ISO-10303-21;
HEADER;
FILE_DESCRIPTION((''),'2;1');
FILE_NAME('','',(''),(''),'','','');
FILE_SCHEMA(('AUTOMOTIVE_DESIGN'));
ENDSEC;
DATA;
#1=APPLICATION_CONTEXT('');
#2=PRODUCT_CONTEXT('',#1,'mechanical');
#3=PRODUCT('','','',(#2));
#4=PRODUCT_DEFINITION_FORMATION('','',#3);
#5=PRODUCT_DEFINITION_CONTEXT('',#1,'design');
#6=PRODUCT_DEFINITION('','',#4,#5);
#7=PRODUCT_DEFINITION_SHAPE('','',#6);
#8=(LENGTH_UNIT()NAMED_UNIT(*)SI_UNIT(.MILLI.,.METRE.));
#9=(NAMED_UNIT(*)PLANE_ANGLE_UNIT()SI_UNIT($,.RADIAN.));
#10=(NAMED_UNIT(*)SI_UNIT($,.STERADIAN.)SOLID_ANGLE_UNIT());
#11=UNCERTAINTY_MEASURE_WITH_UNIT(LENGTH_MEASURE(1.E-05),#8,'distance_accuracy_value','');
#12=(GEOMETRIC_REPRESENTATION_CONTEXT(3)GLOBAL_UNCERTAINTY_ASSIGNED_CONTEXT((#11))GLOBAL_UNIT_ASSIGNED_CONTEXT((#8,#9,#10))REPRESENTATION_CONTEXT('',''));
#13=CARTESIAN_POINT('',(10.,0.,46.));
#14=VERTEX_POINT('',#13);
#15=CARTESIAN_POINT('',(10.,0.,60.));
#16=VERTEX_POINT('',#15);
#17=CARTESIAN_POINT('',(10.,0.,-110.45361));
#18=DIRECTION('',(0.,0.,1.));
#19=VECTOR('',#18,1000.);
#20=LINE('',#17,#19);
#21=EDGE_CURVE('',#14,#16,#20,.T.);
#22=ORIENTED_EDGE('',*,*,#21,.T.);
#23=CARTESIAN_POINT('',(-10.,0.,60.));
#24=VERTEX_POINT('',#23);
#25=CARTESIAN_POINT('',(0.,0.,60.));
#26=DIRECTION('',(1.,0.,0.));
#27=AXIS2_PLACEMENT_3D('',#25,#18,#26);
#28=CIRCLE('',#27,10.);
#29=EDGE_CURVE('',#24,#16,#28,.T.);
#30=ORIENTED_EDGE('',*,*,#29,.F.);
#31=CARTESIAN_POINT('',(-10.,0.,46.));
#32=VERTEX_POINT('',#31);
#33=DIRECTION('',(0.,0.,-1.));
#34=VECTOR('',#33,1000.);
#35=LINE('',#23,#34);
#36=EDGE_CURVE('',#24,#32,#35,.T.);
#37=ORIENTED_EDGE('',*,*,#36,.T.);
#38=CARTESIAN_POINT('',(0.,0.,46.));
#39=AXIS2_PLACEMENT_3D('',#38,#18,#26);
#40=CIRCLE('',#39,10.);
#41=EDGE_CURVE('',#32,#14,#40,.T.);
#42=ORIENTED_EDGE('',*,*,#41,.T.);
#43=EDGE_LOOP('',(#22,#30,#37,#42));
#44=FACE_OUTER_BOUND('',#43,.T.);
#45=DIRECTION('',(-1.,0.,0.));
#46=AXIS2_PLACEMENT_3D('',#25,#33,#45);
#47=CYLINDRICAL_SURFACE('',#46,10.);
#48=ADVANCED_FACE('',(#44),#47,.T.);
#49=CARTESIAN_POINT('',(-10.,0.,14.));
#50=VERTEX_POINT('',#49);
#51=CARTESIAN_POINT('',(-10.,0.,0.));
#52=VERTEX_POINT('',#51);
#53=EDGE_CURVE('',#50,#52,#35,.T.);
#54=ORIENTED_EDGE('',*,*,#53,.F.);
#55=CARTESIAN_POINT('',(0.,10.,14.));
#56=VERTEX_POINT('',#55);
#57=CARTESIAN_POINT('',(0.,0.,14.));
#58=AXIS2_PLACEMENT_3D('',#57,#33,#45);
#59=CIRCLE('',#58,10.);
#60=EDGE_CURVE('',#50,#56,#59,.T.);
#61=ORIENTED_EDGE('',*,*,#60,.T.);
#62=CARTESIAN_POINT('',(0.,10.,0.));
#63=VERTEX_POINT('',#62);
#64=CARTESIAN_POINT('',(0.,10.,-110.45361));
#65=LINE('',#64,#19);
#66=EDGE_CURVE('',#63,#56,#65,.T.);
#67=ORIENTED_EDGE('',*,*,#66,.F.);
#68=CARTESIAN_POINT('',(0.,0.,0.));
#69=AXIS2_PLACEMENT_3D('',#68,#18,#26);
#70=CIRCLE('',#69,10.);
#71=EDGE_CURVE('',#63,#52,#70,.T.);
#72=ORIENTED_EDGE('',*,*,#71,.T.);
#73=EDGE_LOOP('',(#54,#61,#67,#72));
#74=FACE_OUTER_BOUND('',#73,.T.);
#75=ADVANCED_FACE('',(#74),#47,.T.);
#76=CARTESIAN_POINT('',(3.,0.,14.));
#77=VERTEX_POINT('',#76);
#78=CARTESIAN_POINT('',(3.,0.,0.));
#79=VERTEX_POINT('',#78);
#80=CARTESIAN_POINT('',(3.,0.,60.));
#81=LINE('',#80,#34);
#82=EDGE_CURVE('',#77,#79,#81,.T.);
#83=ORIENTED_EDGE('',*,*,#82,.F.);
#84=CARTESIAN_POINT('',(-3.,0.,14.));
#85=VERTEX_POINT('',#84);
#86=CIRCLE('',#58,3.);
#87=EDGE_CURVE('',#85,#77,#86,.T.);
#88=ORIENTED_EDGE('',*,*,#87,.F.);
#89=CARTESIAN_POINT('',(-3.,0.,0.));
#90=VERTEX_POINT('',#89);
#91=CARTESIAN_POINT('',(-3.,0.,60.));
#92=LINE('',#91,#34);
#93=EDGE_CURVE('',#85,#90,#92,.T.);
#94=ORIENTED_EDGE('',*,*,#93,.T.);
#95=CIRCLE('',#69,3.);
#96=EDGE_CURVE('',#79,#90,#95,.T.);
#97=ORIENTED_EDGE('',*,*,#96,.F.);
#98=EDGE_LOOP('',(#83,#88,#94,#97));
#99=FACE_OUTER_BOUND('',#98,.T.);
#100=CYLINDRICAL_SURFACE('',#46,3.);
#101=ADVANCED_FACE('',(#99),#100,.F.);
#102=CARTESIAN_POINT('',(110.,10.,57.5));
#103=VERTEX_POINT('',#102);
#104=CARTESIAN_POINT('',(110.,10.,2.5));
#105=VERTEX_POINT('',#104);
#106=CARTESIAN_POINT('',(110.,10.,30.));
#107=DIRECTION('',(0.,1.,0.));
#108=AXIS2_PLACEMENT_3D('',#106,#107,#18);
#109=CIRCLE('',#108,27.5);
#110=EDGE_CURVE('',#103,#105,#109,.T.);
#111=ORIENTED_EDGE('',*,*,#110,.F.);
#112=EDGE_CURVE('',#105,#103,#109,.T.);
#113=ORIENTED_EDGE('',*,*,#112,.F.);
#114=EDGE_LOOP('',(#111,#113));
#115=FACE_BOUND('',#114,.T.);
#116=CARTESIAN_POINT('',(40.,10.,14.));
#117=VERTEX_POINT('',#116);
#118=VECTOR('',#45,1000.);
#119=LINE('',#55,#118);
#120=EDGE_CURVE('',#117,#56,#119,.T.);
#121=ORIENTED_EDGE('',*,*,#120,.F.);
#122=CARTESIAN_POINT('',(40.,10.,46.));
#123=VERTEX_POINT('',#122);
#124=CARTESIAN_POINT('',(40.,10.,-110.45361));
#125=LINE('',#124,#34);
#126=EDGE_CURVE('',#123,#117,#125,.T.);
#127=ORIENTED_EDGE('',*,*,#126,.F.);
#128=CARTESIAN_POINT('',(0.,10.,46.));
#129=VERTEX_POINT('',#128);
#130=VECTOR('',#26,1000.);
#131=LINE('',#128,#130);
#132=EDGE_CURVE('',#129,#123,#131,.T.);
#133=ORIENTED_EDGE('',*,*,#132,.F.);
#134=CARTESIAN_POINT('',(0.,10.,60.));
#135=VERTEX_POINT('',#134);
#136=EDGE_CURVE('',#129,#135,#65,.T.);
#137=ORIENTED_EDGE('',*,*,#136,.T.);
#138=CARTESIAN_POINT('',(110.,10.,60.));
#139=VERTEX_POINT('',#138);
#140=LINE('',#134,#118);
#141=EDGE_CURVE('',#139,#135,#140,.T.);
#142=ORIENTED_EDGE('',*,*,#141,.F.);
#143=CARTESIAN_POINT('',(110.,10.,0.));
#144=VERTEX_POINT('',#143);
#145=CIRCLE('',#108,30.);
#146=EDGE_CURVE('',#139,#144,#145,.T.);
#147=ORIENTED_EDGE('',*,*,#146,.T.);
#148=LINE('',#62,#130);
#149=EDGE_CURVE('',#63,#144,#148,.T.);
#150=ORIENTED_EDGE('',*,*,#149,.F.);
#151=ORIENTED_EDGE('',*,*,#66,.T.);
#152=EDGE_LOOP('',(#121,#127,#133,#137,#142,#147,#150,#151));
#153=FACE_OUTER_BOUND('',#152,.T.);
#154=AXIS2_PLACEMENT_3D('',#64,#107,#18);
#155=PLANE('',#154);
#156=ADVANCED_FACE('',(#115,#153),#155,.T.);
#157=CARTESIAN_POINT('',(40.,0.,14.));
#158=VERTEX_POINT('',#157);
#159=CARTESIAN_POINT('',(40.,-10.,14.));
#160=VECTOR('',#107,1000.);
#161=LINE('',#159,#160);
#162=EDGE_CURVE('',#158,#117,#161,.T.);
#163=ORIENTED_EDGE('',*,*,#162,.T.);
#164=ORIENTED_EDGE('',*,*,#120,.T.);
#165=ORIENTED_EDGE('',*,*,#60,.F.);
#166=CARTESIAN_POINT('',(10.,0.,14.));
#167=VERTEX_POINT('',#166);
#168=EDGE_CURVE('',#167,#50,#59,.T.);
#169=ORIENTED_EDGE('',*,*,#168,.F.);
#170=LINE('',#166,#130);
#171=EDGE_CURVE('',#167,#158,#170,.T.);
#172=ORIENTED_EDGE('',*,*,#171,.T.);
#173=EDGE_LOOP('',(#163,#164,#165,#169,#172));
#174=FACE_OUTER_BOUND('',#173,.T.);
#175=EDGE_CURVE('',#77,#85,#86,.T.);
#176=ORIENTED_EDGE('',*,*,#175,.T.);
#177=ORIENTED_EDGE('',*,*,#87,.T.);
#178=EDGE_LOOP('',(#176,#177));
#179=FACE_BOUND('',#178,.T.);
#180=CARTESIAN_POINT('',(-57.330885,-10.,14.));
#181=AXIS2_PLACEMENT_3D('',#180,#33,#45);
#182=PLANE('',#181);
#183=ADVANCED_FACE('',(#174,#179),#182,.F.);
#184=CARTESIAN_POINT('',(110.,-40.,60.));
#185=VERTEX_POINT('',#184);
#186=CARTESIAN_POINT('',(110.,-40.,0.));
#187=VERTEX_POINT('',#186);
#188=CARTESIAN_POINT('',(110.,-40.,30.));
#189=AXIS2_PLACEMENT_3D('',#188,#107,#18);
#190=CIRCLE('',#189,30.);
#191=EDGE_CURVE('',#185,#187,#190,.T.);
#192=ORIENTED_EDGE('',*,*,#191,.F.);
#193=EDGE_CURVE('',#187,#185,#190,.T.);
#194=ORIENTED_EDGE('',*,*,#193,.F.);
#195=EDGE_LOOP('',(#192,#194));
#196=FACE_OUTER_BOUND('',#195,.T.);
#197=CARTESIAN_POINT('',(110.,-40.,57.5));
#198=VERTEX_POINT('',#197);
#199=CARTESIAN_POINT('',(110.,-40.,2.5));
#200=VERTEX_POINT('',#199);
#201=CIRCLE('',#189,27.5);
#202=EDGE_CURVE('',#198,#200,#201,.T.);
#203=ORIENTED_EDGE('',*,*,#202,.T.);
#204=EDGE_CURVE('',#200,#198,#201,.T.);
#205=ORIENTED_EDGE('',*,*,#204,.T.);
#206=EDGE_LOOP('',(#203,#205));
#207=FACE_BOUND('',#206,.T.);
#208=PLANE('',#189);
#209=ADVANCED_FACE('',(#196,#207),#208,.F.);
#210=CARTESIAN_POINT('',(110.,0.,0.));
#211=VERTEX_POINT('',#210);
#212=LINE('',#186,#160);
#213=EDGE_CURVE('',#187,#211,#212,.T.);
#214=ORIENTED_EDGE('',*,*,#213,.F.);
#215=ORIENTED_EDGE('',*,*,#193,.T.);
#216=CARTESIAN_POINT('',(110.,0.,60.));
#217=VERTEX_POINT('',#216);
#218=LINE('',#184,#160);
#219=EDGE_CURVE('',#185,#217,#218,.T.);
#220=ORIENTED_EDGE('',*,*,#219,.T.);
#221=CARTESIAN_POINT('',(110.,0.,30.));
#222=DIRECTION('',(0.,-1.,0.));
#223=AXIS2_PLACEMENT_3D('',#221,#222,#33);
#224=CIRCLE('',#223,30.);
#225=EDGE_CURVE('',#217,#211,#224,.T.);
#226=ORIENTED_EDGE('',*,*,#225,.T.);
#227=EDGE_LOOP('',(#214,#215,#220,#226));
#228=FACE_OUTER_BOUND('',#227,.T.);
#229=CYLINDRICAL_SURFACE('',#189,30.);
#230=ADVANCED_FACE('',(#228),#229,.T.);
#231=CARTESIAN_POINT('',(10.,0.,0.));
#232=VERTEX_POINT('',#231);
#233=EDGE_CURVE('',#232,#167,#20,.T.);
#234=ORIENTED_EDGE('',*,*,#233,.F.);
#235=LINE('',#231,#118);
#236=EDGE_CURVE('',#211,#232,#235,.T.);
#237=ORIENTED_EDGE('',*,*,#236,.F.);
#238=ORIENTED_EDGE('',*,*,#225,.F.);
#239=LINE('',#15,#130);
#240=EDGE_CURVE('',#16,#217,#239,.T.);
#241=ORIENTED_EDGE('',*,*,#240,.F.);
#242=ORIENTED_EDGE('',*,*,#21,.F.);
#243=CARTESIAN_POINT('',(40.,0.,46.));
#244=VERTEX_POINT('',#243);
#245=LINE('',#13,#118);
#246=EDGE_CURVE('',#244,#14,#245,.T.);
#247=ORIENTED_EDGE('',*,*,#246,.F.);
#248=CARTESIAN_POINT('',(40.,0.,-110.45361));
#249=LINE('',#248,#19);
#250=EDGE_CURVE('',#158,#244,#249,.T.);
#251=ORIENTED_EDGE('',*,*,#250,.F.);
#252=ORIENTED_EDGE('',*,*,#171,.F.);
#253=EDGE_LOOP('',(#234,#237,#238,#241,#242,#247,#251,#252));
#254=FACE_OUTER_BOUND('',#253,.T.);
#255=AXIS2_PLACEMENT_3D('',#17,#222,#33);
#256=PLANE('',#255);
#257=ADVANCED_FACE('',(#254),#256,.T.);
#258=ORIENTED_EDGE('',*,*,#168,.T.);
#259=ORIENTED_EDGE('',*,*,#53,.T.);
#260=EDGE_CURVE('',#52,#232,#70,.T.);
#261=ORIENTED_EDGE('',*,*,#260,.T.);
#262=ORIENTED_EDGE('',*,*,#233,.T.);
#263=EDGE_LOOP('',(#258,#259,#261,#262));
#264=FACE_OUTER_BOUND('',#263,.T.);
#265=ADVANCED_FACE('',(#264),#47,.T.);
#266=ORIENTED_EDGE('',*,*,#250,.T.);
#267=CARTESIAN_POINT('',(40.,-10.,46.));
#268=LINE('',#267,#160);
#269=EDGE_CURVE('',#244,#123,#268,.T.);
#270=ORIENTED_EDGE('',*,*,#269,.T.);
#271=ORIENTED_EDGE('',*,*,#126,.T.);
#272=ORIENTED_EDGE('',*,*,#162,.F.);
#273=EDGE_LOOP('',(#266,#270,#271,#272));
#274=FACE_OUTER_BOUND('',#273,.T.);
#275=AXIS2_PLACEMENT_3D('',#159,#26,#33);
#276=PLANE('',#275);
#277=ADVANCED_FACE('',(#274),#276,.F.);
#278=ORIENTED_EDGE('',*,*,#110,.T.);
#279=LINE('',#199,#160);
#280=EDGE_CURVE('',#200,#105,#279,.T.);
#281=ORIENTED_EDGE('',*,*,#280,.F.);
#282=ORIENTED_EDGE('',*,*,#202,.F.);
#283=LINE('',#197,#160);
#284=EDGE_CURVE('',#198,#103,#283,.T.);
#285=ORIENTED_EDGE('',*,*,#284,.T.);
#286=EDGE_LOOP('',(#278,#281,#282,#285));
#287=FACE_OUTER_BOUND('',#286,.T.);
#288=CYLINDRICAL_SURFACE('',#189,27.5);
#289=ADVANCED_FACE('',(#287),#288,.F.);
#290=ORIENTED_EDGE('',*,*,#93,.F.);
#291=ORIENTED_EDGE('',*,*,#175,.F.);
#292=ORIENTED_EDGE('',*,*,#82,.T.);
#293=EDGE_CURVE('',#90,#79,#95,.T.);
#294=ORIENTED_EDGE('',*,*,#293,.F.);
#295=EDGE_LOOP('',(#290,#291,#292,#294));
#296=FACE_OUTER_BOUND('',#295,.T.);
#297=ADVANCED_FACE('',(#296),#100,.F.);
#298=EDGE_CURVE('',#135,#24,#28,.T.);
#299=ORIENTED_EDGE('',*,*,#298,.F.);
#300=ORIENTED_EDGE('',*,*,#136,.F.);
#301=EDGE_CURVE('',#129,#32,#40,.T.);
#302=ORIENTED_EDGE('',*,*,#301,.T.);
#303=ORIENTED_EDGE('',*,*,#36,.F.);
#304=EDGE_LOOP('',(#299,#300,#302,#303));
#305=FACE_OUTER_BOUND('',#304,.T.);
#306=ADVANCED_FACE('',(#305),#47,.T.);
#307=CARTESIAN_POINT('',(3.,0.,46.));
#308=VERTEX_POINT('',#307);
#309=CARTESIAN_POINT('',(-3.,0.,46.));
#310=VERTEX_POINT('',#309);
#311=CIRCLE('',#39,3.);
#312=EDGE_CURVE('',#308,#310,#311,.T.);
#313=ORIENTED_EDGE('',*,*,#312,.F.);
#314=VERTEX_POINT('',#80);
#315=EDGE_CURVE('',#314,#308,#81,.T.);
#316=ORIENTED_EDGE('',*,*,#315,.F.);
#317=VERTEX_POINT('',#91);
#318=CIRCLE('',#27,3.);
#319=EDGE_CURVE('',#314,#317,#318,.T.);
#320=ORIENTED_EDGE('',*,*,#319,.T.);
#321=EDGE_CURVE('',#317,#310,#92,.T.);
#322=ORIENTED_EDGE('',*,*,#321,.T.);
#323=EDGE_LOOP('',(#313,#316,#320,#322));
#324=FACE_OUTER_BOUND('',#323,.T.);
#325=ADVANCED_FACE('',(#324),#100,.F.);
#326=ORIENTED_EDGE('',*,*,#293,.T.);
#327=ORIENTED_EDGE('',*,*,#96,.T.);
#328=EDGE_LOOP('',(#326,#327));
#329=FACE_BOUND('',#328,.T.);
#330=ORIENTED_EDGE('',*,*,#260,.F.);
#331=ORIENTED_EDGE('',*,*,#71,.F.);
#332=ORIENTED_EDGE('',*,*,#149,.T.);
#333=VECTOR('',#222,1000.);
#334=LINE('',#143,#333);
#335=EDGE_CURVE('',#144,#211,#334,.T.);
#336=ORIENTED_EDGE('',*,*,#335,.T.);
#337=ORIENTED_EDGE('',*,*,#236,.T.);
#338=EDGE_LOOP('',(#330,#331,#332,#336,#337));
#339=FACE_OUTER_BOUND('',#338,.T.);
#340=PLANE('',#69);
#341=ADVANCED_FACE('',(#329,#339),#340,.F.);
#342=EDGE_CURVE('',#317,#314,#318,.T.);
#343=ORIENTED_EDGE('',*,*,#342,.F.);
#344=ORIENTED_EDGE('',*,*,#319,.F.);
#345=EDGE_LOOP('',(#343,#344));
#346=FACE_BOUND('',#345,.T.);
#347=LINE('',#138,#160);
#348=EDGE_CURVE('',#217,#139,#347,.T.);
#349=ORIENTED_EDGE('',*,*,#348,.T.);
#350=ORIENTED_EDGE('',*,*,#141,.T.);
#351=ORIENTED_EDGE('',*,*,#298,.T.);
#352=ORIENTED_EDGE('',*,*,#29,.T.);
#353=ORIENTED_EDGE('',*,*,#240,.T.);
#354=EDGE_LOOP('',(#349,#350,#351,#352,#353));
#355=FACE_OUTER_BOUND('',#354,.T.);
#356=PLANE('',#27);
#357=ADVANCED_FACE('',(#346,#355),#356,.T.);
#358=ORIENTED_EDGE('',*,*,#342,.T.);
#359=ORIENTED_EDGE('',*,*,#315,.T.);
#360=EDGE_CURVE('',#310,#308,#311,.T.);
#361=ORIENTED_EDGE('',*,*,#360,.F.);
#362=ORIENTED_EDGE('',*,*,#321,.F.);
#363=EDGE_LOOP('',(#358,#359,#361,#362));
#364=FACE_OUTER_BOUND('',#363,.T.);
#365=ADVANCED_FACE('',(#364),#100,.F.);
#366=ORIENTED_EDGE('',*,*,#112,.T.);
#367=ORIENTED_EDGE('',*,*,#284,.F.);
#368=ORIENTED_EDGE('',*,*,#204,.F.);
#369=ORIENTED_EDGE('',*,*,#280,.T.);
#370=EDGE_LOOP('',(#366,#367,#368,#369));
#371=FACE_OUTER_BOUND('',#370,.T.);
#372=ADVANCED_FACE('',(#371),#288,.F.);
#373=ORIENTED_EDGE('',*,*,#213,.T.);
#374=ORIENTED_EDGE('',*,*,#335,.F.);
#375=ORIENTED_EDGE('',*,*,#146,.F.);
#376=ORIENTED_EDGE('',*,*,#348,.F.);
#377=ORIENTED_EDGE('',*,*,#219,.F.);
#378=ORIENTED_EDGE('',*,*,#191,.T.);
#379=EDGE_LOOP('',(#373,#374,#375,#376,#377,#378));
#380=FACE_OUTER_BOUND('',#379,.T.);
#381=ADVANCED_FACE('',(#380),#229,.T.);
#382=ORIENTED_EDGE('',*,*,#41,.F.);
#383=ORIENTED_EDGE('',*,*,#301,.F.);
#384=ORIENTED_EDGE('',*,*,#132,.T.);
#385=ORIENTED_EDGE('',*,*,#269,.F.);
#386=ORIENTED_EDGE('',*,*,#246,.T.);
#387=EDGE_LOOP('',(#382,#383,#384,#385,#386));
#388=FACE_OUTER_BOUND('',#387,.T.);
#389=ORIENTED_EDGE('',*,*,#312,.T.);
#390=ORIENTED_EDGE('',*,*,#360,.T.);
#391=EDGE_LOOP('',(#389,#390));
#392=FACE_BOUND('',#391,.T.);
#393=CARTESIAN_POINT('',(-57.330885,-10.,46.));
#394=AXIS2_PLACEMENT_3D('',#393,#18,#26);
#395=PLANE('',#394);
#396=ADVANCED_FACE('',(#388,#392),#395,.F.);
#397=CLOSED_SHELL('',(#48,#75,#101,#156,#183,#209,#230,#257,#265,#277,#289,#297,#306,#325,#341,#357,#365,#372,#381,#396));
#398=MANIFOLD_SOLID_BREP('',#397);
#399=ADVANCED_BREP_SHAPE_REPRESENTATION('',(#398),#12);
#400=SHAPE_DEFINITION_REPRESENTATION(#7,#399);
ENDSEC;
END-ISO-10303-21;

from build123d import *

# Parameters (mm, degrees)
SKETCH1_R               = 10
SKETCH1_R_2             = 3
BOSS_EXTRUDE1_DEPTH     = 60
BOSS_EXTRUDE2_START     = -60
BOSS_EXTRUDE2_DEPTH     = 60
CUT_EXTRUDE1_DEPTH      = 127.885775404
CUT_EXTRUDE1_DEPTH_BACK = 127.885775404
SKETCH4_W               = 97.330885133
SKETCH4_H               = 32
SKETCH5_R               = 30
SKETCH5_R_2             = 27.5
BOSS_EXTRUDE3_DEPTH     = 50
CUT_EXTRUDE2_DEPTH      = 161.312195419
CUT_EXTRUDE2_DEPTH_BACK = 161.312195419
SKETCH6_R               = 27.5


with BuildPart() as part:
    # Sketch1 → Boss-Extrude1 (new body)
    with BuildSketch(Plane.XY):
        Circle(SKETCH1_R)
        Circle(SKETCH1_R_2, mode=Mode.SUBTRACT)
    extrude(amount=BOSS_EXTRUDE1_DEPTH)

    # Sketch3 → Boss-Extrude2 (add)
    with BuildSketch(Plane.XY.offset(60).offset(BOSS_EXTRUDE2_START)):
        with BuildLine():
            Line((0, 10), (110, 10))
            Line((110, 10), (110, 0))
            Line((110, 0), (10, 0))
            ThreePointArc((10, 0), (7.071067812, 7.071067812), (0, 10))
        make_face()
    extrude(amount=BOSS_EXTRUDE2_DEPTH)

    # Sketch4 → Cut-Extrude1 (cut, two sides: drawn at the far end of the back side and taken through both)
    with BuildSketch(Plane(origin=(0, 10, 0), x_dir=(1, 0, 0), z_dir=(0, 1, 0)).offset(-CUT_EXTRUDE1_DEPTH_BACK)):
        with Locations((-8.665442567, -30)):
            Rectangle(SKETCH4_W, SKETCH4_H)
    extrude(amount=CUT_EXTRUDE1_DEPTH + CUT_EXTRUDE1_DEPTH_BACK, mode=Mode.SUBTRACT)

    # Sketch5 → Boss-Extrude3 (add)
    with BuildSketch(Plane(origin=(0, 10, 0), x_dir=(1, 0, 0), z_dir=(0, 1, 0))):
        with Locations(Location((110, -30, 0), (0, 0, 270))):
            Circle(SKETCH5_R)
        with Locations(Location((110, -30, 0), (0, 0, 270))):
            Circle(SKETCH5_R_2, mode=Mode.SUBTRACT)
    extrude(amount=-BOSS_EXTRUDE3_DEPTH)

    # Sketch6 → Cut-Extrude2 (cut, two sides: drawn at the far end of the back side and taken through both)
    with BuildSketch(Plane(origin=(0, 10, 0), x_dir=(1, 0, 0), z_dir=(0, 1, 0)).offset(-CUT_EXTRUDE2_DEPTH_BACK)):
        with Locations(Location((110, -30, 0), (0, 0, 270))):
            Circle(SKETCH6_R)
    extrude(amount=CUT_EXTRUDE2_DEPTH + CUT_EXTRUDE2_DEPTH_BACK, mode=Mode.SUBTRACT)


solid = part.part
